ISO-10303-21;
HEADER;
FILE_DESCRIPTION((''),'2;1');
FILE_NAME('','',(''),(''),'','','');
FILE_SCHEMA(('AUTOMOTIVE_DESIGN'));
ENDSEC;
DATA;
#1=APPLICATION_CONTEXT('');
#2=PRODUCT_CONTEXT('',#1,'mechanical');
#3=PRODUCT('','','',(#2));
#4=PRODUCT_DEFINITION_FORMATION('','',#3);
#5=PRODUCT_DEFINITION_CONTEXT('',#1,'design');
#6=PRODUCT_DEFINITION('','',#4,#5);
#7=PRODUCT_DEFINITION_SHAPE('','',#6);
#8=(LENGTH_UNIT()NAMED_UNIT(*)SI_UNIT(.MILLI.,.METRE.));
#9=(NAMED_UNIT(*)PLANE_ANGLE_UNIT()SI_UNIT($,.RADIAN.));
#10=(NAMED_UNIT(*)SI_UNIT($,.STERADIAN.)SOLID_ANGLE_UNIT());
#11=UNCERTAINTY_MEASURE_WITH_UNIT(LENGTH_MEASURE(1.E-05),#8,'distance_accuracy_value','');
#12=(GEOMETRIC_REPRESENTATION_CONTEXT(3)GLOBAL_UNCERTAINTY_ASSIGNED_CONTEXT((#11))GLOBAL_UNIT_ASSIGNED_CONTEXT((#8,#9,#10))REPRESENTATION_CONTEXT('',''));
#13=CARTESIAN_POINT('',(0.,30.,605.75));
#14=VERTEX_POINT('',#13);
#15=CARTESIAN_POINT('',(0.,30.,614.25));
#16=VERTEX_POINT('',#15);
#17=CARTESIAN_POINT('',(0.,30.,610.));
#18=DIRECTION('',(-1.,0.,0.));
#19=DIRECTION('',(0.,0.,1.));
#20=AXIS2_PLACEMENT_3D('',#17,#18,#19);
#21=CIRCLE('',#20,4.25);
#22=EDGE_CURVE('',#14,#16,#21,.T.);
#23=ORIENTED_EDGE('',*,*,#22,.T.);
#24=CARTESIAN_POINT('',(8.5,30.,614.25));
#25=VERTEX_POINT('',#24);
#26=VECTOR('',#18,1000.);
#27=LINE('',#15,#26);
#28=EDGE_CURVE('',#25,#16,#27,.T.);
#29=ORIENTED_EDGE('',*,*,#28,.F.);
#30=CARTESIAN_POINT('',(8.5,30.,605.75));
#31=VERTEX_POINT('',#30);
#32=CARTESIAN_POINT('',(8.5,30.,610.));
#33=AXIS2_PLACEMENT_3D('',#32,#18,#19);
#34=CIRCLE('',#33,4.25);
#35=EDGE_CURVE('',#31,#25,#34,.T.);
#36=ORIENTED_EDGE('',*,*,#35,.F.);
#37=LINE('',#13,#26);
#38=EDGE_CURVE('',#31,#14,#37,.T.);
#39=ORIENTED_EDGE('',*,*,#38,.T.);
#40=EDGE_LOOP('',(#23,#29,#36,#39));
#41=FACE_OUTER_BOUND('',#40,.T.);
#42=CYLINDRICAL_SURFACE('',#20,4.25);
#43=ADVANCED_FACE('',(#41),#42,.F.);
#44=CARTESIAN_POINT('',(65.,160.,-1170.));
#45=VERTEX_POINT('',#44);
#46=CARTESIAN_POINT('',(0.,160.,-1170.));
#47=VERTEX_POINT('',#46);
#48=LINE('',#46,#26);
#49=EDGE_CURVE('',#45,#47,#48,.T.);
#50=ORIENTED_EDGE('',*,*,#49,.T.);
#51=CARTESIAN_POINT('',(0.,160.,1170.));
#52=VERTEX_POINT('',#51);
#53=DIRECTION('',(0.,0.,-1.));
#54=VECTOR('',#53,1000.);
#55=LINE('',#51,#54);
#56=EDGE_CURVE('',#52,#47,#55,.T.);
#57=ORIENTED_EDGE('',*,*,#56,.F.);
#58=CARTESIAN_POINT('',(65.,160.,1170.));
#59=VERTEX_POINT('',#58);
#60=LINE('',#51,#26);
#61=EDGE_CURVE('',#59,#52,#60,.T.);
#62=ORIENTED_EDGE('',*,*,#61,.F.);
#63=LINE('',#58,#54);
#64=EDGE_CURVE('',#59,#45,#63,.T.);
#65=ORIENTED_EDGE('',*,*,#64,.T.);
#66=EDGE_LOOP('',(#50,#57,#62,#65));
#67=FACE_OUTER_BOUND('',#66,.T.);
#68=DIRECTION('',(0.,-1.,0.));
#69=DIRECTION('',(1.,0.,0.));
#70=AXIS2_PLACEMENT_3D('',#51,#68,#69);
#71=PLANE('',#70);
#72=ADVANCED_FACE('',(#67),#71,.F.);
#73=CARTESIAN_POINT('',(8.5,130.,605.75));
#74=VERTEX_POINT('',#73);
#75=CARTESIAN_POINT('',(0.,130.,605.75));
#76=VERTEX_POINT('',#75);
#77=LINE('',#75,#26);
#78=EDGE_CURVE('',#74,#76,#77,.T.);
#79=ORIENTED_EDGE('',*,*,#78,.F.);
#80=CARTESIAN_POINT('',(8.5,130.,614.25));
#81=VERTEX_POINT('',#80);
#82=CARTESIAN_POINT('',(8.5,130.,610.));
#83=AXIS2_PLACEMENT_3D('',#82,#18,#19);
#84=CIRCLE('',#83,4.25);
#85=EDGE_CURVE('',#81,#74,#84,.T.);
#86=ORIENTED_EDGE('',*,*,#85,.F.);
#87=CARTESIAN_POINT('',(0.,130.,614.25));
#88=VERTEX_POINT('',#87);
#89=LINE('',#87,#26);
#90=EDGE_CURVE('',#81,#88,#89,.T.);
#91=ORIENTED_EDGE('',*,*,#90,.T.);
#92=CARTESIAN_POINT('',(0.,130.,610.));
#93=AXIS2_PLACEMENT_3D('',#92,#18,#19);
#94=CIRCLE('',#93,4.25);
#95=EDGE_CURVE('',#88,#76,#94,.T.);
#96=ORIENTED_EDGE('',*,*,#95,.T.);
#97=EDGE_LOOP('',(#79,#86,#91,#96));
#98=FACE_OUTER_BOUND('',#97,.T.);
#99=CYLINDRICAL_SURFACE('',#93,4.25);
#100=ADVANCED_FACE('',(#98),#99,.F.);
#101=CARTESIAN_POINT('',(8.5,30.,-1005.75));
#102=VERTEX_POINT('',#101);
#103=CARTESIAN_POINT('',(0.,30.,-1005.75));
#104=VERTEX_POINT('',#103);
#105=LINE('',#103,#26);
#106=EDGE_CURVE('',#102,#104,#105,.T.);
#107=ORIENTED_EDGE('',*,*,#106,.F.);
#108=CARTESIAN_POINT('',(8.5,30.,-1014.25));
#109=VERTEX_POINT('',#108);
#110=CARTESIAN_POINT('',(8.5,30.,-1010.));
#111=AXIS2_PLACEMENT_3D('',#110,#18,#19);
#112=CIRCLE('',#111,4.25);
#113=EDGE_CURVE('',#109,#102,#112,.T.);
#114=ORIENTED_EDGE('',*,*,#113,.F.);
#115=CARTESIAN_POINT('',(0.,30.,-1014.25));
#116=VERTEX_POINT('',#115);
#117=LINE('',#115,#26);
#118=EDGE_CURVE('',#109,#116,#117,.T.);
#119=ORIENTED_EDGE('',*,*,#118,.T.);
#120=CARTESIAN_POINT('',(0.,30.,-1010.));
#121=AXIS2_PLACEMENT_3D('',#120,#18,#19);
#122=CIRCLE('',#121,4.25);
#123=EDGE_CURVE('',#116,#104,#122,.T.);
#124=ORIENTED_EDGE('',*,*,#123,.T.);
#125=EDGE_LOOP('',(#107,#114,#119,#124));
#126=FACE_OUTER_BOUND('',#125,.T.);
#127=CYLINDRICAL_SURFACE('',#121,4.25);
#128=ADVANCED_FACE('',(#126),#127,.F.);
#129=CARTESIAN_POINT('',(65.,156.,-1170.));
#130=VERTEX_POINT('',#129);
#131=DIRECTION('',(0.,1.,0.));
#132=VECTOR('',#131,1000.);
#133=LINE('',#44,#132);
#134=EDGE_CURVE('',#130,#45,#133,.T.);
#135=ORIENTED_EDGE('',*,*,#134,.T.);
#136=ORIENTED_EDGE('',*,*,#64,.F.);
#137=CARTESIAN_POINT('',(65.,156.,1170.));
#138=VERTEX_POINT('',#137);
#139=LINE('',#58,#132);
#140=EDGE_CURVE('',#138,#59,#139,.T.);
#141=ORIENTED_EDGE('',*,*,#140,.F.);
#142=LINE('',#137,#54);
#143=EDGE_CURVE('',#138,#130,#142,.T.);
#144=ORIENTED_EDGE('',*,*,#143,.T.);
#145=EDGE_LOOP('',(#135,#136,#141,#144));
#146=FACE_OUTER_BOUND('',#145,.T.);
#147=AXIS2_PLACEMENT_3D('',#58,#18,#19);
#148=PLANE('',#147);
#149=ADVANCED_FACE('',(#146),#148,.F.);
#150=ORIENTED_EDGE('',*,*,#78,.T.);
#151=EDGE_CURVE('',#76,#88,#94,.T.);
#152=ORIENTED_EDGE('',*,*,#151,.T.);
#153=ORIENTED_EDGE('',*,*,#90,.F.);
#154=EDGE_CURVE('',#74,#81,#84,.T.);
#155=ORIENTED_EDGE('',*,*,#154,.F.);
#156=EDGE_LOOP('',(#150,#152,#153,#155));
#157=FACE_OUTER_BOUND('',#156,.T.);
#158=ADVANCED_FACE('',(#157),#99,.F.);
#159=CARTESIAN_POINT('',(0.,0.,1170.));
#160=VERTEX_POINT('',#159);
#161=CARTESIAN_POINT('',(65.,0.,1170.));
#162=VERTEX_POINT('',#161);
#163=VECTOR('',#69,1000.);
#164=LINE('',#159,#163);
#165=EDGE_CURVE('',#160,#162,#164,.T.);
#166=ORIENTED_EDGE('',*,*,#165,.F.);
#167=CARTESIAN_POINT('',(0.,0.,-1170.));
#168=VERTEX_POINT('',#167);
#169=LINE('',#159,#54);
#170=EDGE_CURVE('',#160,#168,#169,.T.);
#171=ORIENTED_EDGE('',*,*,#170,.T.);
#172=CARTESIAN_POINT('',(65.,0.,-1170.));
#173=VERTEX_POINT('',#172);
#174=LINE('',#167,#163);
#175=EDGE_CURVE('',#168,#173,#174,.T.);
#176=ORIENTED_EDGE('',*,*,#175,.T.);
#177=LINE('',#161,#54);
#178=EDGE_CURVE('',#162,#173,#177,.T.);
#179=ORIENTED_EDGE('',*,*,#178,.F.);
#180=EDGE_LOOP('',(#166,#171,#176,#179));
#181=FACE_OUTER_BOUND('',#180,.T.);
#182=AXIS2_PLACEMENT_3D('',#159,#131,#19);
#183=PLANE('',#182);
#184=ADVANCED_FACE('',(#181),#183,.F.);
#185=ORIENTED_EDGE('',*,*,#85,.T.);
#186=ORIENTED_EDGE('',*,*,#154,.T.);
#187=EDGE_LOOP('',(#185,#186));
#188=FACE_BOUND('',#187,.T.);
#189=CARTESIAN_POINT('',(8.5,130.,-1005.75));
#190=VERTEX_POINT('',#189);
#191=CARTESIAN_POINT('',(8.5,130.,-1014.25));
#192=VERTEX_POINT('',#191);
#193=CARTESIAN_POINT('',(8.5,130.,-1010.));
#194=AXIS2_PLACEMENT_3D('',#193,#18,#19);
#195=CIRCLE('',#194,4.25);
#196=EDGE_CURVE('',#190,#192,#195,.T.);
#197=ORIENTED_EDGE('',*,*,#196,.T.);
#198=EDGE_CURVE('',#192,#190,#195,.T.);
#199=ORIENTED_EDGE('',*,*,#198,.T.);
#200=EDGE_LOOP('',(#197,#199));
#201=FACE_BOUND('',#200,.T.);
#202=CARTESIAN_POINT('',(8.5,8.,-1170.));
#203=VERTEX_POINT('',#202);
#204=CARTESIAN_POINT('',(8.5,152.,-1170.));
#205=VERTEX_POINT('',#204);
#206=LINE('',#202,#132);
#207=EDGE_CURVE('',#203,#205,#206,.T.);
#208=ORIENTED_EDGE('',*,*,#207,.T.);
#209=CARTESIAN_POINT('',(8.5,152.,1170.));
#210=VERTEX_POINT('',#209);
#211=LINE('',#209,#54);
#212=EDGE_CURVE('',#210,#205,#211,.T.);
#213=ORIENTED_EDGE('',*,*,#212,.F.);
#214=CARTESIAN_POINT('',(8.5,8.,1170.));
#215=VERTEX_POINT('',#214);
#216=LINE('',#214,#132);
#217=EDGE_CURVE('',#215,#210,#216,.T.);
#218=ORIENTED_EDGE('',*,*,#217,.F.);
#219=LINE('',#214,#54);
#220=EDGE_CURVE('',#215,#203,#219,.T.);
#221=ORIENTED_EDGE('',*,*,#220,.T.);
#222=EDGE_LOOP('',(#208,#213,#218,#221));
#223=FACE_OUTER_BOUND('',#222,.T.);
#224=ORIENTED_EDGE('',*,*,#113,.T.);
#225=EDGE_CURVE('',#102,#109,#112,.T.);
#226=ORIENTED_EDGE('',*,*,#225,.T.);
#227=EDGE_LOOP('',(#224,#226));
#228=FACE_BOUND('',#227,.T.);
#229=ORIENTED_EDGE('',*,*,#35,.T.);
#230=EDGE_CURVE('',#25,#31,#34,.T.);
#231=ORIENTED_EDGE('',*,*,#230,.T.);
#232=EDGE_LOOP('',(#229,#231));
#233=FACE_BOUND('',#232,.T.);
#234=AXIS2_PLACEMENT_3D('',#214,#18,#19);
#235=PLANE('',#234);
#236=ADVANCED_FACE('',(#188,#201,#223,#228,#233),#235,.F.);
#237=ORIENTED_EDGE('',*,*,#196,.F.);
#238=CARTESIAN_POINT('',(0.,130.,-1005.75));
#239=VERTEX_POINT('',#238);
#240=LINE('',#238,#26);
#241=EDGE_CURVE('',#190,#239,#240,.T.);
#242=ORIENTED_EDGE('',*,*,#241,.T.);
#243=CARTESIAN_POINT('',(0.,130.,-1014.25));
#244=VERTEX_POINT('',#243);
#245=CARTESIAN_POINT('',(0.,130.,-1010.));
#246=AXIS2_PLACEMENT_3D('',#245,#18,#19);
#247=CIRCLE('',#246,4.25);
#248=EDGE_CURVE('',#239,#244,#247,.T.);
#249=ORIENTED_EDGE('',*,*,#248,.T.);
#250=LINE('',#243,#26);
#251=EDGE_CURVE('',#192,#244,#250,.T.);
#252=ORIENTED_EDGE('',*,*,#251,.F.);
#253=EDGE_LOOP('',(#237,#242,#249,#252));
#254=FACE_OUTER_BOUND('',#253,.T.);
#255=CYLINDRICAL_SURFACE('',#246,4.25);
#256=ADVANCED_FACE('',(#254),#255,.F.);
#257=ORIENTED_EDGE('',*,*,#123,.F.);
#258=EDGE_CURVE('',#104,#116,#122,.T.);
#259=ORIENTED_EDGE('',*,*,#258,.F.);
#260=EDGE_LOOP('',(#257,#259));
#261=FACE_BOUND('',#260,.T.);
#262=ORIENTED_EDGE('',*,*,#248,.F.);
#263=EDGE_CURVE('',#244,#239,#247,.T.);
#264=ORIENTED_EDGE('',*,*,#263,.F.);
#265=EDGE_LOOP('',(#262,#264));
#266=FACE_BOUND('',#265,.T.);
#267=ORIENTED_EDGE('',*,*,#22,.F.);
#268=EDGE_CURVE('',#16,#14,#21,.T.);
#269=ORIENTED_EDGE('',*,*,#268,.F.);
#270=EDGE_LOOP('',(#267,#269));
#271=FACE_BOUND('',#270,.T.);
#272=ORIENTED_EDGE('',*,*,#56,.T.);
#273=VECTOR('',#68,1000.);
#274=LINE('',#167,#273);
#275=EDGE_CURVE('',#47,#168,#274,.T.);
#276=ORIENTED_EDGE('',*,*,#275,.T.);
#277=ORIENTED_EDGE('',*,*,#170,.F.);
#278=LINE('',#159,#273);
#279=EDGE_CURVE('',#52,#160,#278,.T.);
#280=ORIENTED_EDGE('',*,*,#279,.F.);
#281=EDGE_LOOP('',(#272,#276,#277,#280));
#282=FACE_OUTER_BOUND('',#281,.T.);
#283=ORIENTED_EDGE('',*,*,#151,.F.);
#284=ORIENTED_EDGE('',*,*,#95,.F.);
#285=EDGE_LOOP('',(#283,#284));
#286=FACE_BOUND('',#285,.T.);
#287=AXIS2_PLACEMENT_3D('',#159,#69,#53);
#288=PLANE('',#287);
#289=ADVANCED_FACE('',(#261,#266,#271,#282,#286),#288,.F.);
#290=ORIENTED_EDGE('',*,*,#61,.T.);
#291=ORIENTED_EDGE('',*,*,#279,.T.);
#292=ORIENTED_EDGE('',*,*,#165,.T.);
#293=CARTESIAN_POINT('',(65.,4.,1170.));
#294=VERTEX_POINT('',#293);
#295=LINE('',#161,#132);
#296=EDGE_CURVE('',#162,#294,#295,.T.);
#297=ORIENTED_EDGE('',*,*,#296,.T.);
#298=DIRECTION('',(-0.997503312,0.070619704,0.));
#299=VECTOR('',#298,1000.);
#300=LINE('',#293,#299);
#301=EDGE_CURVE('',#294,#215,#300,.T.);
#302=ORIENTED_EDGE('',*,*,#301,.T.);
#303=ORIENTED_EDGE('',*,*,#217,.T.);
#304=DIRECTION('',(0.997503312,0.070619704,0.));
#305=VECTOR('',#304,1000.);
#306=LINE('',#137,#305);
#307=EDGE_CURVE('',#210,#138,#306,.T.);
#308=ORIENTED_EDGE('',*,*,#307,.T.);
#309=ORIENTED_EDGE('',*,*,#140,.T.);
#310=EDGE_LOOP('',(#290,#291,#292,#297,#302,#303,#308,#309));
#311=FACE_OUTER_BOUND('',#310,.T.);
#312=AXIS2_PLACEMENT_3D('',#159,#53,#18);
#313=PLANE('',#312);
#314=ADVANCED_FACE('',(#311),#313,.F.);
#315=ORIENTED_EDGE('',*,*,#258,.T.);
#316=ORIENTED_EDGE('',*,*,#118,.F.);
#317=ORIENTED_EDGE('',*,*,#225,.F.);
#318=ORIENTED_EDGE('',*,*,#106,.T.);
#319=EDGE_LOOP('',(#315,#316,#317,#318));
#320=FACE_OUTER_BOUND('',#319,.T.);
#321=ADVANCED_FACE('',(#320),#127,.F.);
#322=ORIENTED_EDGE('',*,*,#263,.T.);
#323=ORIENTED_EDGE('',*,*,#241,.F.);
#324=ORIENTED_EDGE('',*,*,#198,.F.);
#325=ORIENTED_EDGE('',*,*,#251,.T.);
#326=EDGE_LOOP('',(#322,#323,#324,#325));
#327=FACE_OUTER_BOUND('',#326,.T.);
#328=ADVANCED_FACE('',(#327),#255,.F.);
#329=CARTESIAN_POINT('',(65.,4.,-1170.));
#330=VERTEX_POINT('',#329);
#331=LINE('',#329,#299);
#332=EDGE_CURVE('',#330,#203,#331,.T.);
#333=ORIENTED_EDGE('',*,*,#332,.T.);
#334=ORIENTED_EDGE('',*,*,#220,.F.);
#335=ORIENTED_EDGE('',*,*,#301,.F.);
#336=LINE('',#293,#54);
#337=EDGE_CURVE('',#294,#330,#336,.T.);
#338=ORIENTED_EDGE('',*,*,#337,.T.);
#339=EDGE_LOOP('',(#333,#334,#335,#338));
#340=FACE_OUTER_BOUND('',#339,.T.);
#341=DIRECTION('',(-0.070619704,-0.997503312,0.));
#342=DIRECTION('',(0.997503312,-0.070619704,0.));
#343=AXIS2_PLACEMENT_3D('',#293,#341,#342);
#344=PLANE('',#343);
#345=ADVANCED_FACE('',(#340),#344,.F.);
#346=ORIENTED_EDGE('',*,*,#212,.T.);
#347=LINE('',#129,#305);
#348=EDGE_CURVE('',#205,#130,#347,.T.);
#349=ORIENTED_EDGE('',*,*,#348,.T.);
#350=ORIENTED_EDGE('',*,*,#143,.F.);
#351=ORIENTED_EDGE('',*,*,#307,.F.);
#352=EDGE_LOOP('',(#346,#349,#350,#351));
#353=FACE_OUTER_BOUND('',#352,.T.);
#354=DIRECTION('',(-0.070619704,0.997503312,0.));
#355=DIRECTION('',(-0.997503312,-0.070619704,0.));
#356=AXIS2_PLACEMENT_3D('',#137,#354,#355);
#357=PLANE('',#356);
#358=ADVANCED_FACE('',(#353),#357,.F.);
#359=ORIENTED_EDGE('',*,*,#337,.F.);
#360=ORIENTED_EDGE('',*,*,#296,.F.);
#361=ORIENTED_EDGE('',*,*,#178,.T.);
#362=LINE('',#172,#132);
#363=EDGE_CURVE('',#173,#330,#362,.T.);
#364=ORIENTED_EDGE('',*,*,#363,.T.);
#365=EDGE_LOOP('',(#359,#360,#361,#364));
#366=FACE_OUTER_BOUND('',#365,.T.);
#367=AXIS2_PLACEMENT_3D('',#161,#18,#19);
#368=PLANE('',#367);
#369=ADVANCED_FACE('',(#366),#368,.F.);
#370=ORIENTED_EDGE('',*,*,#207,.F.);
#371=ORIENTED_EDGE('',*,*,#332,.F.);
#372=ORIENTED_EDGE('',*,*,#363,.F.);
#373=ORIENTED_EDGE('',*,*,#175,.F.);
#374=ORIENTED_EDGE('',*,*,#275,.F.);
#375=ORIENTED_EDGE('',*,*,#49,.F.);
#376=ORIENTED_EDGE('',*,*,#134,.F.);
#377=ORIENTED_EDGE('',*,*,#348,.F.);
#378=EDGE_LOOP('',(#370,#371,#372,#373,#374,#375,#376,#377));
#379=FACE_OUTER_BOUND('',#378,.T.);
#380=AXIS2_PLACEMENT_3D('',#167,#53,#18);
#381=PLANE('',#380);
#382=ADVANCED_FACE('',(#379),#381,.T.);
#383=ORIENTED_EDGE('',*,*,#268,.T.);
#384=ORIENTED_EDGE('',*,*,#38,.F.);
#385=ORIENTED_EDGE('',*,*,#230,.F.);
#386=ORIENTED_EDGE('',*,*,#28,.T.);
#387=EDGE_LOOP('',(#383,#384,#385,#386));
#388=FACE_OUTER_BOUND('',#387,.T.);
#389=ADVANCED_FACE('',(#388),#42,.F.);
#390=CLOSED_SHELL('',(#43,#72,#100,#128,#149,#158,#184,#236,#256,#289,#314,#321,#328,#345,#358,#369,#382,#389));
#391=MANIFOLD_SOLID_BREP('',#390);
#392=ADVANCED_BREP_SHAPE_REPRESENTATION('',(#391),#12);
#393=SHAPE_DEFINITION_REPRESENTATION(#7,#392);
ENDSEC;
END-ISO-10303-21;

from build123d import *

# Parameters (mm, degrees)
EXTRUDE_1_DEPTH         = 1170
HOLE_WIZARD_M10_1_D     = 8.5
HOLE_WIZARD_M10_1_DEPTH = 27.5
HOLE_WIZARD_M10_1_TIP   = 2.553657631


with BuildPart() as part:
    # 草图1 → 凸台-拉伸1 (new, symmetric)
    with BuildSketch(Plane.XY):
        Polygon((0, 0), (65, 0), (65, 4), (8.5, 8), (8.5, 152), (65, 156), (65, 160), (0, 160), align=None)
    extrude(amount=EXTRUDE_1_DEPTH, both=True)

    # M10 螺纹孔1
    with Locations(Plane.ZY):
        with Locations((-1010, 30), (610, 30), (-1010, 130), (610, 130)):
            Hole(HOLE_WIZARD_M10_1_D / 2, depth=HOLE_WIZARD_M10_1_DEPTH)
            with Locations((0, 0, -(HOLE_WIZARD_M10_1_DEPTH + HOLE_WIZARD_M10_1_TIP / 2))):  # 118° drill point
                Cone(0, HOLE_WIZARD_M10_1_D / 2, HOLE_WIZARD_M10_1_TIP, mode=Mode.SUBTRACT)


solid = part.part
